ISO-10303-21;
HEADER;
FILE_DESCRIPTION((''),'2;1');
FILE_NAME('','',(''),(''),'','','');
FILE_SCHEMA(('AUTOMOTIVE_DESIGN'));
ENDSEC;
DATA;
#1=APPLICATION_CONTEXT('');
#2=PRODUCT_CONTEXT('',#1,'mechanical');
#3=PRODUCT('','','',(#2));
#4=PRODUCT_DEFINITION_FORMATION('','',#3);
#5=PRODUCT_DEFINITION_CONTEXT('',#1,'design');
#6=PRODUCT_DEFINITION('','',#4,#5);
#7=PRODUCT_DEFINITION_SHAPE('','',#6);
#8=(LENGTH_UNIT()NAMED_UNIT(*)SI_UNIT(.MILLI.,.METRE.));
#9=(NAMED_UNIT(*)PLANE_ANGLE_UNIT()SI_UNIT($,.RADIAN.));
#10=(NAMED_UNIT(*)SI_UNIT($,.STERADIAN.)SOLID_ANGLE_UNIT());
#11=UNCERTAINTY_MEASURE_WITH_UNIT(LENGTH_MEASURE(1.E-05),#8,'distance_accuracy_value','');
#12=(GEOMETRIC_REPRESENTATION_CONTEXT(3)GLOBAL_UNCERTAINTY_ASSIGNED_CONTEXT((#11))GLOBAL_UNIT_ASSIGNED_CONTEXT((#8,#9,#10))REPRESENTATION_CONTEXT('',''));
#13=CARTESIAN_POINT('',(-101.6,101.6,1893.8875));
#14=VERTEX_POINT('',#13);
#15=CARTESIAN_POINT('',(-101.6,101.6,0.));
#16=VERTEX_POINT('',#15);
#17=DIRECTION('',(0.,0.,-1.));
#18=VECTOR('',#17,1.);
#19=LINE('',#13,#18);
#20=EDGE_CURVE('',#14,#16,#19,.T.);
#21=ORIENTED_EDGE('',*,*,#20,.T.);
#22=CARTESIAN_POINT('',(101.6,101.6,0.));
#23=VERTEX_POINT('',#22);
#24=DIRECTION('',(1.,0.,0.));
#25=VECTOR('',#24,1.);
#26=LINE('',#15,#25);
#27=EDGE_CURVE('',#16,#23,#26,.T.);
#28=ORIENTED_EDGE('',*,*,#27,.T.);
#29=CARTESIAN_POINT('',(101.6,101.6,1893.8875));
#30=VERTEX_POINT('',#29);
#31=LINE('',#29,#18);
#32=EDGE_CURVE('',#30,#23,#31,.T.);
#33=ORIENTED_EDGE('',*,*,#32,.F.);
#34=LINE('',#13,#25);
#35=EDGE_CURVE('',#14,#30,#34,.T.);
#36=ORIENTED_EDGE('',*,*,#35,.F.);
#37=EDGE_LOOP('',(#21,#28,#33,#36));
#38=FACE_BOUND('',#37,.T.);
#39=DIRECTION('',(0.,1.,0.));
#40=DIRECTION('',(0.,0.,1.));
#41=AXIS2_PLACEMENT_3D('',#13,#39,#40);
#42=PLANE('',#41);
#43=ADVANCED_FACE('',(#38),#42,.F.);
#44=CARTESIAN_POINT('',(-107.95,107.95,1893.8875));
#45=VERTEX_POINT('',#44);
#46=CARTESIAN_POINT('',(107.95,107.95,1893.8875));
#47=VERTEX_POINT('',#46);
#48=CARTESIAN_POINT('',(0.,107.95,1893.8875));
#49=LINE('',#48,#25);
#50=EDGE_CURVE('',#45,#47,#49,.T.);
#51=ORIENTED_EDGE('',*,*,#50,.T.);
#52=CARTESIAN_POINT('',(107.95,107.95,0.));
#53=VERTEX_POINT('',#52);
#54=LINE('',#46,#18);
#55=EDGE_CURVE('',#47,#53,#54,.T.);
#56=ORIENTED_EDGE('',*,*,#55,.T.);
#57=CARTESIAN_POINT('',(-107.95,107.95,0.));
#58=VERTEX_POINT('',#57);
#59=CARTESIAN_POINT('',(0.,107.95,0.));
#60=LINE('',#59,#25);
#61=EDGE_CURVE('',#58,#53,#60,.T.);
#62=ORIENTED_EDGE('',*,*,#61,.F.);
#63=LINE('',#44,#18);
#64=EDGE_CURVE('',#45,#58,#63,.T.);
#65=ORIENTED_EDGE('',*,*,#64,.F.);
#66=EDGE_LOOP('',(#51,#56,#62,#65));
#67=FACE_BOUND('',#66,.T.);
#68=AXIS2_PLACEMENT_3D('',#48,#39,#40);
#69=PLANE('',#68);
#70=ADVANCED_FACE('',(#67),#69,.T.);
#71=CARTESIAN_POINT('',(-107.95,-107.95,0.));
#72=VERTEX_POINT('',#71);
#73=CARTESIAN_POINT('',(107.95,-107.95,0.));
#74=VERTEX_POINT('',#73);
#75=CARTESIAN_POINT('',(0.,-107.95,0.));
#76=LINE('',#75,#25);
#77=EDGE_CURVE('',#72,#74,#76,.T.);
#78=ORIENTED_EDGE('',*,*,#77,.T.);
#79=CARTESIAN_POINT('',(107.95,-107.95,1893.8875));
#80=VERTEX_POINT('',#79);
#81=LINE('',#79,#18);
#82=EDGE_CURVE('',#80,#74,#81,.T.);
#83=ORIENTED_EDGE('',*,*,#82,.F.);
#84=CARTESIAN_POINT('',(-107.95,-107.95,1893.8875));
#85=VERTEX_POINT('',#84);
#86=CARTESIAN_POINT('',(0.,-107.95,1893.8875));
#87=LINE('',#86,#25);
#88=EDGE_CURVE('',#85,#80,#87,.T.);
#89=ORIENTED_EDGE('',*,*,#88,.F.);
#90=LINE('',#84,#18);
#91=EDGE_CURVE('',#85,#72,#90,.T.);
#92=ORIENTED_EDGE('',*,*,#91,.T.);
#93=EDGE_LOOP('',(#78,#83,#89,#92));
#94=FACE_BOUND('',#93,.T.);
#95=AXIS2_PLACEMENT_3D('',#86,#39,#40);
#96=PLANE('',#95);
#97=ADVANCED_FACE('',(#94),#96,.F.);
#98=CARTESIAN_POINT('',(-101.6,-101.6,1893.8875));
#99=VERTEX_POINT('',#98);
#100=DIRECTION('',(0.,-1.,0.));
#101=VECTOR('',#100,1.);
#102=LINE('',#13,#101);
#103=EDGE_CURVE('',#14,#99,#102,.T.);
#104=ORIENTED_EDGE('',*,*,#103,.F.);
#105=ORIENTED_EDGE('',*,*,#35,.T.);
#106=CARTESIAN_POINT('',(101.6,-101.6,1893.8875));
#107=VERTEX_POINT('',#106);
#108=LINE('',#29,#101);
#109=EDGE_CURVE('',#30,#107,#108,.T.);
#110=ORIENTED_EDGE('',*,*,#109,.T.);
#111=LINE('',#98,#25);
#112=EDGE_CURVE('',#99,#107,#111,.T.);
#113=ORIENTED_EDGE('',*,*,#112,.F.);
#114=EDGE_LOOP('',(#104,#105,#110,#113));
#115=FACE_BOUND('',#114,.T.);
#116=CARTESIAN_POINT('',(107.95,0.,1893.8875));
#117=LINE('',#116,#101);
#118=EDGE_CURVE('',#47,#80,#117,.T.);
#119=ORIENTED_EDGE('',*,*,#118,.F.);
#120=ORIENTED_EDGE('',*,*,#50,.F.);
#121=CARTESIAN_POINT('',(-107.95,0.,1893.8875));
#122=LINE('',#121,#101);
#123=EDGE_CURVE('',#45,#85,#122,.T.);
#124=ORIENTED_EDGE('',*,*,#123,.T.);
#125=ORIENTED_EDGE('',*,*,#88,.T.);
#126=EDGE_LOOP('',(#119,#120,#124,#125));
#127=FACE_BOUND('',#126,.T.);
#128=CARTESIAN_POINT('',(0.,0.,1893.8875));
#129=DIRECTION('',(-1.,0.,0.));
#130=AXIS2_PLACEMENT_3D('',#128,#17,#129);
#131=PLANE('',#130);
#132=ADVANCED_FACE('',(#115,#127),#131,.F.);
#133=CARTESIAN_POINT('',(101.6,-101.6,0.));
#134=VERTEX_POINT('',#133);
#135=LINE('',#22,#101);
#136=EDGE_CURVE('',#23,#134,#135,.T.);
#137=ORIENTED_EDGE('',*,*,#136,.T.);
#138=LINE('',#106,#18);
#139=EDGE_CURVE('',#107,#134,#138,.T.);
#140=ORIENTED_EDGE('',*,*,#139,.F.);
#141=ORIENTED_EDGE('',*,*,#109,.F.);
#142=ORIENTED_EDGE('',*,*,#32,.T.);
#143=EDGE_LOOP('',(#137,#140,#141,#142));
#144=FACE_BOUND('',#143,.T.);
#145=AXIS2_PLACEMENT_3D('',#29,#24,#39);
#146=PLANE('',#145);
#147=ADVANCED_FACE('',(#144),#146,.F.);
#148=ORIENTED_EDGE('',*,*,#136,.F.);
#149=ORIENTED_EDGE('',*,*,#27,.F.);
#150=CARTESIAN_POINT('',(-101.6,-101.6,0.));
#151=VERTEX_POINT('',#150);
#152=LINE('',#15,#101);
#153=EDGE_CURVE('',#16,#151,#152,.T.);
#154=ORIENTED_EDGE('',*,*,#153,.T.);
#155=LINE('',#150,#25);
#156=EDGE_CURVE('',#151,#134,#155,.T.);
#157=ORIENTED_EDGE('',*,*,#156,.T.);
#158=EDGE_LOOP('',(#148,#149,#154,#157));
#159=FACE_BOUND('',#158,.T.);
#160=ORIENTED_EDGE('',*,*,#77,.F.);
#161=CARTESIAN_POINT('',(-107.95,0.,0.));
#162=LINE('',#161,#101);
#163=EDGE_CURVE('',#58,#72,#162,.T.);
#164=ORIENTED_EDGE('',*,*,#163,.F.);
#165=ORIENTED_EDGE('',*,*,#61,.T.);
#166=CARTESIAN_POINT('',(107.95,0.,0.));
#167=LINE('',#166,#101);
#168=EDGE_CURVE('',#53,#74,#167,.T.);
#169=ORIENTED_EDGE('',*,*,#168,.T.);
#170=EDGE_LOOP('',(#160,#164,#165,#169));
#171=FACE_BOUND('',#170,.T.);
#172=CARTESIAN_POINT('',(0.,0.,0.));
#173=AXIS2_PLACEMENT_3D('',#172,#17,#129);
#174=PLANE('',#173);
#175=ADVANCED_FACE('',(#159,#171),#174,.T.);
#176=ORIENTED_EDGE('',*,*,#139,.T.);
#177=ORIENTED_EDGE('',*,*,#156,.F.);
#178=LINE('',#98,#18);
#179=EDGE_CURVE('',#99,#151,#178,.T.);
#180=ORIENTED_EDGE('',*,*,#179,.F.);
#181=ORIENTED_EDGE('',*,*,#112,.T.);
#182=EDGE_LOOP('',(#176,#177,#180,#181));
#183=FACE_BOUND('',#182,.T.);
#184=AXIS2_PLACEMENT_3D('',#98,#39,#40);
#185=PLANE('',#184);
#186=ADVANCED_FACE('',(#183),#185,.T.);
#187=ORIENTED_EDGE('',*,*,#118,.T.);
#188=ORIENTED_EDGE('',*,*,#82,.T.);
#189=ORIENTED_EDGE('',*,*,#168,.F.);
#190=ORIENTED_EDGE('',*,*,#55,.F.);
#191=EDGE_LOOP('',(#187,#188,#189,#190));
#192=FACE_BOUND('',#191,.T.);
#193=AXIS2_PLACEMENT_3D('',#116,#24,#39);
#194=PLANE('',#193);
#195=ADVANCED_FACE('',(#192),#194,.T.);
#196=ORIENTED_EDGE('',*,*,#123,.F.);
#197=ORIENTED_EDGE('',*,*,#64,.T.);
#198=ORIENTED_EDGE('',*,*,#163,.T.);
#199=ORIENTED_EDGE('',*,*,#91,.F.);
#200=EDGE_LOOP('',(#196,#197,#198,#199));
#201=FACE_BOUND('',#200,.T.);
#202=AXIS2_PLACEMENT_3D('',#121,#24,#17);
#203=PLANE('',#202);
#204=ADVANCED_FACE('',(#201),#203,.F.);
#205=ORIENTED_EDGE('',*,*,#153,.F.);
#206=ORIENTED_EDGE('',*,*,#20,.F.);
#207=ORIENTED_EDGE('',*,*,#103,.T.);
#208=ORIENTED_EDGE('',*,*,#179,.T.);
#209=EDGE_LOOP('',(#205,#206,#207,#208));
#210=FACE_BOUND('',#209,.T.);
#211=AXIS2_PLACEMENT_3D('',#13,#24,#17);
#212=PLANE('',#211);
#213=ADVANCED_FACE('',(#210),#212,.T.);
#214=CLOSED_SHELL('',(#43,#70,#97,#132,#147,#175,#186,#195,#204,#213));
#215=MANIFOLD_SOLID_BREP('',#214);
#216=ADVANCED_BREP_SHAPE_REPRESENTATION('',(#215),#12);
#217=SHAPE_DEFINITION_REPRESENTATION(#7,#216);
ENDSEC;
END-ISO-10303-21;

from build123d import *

# Parameters (mm, degrees)
TUBE_PROFILE_8X8_SQUARE_W           = 215.9
TUBE_PROFILE_8X8_SQUARE_H           = 215.9
TUBE_PROFILE_8X8_SQUARE_W_2         = 203.2
TUBE_PROFILE_8X8_SQUARE_H_2         = 203.2
SQUARE_TUBE_8_5X8_5X0_25_WALL_DEPTH = 1893.8875


with BuildPart() as part:
    # Tube Profile 8x8 Square → Square Tube 8.5x8.5x0.25 Wall (new body)
    with BuildSketch(Plane.XY):
        Rectangle(TUBE_PROFILE_8X8_SQUARE_W, TUBE_PROFILE_8X8_SQUARE_H)
        Rectangle(TUBE_PROFILE_8X8_SQUARE_W_2, TUBE_PROFILE_8X8_SQUARE_H_2, mode=Mode.SUBTRACT)
    extrude(amount=SQUARE_TUBE_8_5X8_5X0_25_WALL_DEPTH)


solid = part.part
